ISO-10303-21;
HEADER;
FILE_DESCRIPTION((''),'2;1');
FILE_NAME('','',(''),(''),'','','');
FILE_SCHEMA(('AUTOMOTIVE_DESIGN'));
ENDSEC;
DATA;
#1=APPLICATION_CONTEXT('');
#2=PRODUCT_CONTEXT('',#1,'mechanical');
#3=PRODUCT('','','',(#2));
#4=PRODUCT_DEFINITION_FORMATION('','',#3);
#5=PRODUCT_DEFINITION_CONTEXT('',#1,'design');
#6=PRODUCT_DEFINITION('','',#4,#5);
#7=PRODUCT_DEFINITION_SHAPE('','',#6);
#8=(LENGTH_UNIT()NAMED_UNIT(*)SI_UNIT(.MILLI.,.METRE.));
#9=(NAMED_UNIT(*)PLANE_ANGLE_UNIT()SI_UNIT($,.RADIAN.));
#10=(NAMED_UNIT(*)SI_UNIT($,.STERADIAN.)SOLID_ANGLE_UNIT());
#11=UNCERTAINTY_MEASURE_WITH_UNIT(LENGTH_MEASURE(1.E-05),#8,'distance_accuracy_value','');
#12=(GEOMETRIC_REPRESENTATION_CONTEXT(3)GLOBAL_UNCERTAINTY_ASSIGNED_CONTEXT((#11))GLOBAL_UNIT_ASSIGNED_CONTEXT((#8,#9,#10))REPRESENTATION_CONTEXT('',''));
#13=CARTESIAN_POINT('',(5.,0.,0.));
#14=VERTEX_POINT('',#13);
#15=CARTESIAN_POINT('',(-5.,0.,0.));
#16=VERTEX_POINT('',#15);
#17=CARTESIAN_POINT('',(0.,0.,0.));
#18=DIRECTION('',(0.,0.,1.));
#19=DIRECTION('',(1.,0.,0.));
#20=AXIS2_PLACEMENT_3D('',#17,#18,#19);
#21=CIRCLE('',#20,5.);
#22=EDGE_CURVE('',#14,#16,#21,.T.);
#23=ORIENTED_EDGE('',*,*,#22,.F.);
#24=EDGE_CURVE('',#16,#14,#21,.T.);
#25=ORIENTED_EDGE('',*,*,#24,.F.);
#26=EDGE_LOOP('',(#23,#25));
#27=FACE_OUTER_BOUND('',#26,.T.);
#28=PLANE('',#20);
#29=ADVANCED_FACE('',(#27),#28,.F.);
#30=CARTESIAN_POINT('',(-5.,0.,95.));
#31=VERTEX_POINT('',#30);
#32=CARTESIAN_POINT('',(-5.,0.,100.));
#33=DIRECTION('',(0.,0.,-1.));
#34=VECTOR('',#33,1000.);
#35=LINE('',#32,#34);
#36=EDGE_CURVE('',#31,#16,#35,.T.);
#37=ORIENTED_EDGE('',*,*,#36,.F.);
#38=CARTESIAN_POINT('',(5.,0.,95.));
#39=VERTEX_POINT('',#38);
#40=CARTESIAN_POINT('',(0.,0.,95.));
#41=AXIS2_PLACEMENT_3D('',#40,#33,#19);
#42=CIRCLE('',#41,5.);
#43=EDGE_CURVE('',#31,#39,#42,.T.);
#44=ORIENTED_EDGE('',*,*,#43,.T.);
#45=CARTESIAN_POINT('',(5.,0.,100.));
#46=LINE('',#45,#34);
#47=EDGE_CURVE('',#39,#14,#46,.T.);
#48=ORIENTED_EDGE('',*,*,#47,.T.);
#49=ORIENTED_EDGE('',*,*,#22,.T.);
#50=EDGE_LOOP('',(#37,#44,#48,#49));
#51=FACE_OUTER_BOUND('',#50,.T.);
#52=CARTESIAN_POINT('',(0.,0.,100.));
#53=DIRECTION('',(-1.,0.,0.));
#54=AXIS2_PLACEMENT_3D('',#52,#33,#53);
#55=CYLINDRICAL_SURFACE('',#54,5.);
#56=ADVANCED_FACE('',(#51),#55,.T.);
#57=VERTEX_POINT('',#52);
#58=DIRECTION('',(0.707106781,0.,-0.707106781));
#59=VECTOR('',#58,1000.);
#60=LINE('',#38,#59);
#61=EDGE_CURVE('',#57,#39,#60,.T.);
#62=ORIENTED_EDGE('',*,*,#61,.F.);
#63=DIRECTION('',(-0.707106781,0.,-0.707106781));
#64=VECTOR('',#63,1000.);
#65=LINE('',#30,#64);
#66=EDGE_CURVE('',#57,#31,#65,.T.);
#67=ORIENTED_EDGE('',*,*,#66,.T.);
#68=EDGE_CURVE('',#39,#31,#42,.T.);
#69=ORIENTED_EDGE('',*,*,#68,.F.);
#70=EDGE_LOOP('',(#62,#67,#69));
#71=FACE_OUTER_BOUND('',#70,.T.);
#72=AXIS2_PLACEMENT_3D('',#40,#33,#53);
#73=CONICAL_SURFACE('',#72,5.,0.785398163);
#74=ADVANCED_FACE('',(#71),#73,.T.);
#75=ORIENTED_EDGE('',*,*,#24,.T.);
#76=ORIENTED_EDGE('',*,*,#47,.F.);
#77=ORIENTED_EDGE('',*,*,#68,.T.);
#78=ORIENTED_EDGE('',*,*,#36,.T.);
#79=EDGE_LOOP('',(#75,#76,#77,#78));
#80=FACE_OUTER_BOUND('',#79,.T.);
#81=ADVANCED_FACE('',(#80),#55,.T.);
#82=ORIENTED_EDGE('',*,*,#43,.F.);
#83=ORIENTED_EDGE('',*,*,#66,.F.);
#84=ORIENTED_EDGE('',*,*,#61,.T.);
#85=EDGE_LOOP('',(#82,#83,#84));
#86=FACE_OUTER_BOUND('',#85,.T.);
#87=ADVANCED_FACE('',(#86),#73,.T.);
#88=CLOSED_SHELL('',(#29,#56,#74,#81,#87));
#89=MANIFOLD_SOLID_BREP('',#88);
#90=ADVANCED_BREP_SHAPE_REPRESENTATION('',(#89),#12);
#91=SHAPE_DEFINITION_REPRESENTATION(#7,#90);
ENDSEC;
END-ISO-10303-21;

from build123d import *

# Parameters (mm, degrees)
SKETCH1_R           = 5
BOSS_EXTRUDE1_DEPTH = 100
CHAMFER2_SIZE       = 5


with BuildPart() as part:
    # Sketch1 → Boss-Extrude1 (new body)
    with BuildSketch(Plane.XY):
        Circle(SKETCH1_R)
    extrude(amount=BOSS_EXTRUDE1_DEPTH)

    # Chamfer2
    chamfer2_edges = [part.edges().sort_by_distance(p)[0] for p in [
        (-5, 0, 100),
    ]]
    chamfer(chamfer2_edges, length=CHAMFER2_SIZE)


solid = part.part
